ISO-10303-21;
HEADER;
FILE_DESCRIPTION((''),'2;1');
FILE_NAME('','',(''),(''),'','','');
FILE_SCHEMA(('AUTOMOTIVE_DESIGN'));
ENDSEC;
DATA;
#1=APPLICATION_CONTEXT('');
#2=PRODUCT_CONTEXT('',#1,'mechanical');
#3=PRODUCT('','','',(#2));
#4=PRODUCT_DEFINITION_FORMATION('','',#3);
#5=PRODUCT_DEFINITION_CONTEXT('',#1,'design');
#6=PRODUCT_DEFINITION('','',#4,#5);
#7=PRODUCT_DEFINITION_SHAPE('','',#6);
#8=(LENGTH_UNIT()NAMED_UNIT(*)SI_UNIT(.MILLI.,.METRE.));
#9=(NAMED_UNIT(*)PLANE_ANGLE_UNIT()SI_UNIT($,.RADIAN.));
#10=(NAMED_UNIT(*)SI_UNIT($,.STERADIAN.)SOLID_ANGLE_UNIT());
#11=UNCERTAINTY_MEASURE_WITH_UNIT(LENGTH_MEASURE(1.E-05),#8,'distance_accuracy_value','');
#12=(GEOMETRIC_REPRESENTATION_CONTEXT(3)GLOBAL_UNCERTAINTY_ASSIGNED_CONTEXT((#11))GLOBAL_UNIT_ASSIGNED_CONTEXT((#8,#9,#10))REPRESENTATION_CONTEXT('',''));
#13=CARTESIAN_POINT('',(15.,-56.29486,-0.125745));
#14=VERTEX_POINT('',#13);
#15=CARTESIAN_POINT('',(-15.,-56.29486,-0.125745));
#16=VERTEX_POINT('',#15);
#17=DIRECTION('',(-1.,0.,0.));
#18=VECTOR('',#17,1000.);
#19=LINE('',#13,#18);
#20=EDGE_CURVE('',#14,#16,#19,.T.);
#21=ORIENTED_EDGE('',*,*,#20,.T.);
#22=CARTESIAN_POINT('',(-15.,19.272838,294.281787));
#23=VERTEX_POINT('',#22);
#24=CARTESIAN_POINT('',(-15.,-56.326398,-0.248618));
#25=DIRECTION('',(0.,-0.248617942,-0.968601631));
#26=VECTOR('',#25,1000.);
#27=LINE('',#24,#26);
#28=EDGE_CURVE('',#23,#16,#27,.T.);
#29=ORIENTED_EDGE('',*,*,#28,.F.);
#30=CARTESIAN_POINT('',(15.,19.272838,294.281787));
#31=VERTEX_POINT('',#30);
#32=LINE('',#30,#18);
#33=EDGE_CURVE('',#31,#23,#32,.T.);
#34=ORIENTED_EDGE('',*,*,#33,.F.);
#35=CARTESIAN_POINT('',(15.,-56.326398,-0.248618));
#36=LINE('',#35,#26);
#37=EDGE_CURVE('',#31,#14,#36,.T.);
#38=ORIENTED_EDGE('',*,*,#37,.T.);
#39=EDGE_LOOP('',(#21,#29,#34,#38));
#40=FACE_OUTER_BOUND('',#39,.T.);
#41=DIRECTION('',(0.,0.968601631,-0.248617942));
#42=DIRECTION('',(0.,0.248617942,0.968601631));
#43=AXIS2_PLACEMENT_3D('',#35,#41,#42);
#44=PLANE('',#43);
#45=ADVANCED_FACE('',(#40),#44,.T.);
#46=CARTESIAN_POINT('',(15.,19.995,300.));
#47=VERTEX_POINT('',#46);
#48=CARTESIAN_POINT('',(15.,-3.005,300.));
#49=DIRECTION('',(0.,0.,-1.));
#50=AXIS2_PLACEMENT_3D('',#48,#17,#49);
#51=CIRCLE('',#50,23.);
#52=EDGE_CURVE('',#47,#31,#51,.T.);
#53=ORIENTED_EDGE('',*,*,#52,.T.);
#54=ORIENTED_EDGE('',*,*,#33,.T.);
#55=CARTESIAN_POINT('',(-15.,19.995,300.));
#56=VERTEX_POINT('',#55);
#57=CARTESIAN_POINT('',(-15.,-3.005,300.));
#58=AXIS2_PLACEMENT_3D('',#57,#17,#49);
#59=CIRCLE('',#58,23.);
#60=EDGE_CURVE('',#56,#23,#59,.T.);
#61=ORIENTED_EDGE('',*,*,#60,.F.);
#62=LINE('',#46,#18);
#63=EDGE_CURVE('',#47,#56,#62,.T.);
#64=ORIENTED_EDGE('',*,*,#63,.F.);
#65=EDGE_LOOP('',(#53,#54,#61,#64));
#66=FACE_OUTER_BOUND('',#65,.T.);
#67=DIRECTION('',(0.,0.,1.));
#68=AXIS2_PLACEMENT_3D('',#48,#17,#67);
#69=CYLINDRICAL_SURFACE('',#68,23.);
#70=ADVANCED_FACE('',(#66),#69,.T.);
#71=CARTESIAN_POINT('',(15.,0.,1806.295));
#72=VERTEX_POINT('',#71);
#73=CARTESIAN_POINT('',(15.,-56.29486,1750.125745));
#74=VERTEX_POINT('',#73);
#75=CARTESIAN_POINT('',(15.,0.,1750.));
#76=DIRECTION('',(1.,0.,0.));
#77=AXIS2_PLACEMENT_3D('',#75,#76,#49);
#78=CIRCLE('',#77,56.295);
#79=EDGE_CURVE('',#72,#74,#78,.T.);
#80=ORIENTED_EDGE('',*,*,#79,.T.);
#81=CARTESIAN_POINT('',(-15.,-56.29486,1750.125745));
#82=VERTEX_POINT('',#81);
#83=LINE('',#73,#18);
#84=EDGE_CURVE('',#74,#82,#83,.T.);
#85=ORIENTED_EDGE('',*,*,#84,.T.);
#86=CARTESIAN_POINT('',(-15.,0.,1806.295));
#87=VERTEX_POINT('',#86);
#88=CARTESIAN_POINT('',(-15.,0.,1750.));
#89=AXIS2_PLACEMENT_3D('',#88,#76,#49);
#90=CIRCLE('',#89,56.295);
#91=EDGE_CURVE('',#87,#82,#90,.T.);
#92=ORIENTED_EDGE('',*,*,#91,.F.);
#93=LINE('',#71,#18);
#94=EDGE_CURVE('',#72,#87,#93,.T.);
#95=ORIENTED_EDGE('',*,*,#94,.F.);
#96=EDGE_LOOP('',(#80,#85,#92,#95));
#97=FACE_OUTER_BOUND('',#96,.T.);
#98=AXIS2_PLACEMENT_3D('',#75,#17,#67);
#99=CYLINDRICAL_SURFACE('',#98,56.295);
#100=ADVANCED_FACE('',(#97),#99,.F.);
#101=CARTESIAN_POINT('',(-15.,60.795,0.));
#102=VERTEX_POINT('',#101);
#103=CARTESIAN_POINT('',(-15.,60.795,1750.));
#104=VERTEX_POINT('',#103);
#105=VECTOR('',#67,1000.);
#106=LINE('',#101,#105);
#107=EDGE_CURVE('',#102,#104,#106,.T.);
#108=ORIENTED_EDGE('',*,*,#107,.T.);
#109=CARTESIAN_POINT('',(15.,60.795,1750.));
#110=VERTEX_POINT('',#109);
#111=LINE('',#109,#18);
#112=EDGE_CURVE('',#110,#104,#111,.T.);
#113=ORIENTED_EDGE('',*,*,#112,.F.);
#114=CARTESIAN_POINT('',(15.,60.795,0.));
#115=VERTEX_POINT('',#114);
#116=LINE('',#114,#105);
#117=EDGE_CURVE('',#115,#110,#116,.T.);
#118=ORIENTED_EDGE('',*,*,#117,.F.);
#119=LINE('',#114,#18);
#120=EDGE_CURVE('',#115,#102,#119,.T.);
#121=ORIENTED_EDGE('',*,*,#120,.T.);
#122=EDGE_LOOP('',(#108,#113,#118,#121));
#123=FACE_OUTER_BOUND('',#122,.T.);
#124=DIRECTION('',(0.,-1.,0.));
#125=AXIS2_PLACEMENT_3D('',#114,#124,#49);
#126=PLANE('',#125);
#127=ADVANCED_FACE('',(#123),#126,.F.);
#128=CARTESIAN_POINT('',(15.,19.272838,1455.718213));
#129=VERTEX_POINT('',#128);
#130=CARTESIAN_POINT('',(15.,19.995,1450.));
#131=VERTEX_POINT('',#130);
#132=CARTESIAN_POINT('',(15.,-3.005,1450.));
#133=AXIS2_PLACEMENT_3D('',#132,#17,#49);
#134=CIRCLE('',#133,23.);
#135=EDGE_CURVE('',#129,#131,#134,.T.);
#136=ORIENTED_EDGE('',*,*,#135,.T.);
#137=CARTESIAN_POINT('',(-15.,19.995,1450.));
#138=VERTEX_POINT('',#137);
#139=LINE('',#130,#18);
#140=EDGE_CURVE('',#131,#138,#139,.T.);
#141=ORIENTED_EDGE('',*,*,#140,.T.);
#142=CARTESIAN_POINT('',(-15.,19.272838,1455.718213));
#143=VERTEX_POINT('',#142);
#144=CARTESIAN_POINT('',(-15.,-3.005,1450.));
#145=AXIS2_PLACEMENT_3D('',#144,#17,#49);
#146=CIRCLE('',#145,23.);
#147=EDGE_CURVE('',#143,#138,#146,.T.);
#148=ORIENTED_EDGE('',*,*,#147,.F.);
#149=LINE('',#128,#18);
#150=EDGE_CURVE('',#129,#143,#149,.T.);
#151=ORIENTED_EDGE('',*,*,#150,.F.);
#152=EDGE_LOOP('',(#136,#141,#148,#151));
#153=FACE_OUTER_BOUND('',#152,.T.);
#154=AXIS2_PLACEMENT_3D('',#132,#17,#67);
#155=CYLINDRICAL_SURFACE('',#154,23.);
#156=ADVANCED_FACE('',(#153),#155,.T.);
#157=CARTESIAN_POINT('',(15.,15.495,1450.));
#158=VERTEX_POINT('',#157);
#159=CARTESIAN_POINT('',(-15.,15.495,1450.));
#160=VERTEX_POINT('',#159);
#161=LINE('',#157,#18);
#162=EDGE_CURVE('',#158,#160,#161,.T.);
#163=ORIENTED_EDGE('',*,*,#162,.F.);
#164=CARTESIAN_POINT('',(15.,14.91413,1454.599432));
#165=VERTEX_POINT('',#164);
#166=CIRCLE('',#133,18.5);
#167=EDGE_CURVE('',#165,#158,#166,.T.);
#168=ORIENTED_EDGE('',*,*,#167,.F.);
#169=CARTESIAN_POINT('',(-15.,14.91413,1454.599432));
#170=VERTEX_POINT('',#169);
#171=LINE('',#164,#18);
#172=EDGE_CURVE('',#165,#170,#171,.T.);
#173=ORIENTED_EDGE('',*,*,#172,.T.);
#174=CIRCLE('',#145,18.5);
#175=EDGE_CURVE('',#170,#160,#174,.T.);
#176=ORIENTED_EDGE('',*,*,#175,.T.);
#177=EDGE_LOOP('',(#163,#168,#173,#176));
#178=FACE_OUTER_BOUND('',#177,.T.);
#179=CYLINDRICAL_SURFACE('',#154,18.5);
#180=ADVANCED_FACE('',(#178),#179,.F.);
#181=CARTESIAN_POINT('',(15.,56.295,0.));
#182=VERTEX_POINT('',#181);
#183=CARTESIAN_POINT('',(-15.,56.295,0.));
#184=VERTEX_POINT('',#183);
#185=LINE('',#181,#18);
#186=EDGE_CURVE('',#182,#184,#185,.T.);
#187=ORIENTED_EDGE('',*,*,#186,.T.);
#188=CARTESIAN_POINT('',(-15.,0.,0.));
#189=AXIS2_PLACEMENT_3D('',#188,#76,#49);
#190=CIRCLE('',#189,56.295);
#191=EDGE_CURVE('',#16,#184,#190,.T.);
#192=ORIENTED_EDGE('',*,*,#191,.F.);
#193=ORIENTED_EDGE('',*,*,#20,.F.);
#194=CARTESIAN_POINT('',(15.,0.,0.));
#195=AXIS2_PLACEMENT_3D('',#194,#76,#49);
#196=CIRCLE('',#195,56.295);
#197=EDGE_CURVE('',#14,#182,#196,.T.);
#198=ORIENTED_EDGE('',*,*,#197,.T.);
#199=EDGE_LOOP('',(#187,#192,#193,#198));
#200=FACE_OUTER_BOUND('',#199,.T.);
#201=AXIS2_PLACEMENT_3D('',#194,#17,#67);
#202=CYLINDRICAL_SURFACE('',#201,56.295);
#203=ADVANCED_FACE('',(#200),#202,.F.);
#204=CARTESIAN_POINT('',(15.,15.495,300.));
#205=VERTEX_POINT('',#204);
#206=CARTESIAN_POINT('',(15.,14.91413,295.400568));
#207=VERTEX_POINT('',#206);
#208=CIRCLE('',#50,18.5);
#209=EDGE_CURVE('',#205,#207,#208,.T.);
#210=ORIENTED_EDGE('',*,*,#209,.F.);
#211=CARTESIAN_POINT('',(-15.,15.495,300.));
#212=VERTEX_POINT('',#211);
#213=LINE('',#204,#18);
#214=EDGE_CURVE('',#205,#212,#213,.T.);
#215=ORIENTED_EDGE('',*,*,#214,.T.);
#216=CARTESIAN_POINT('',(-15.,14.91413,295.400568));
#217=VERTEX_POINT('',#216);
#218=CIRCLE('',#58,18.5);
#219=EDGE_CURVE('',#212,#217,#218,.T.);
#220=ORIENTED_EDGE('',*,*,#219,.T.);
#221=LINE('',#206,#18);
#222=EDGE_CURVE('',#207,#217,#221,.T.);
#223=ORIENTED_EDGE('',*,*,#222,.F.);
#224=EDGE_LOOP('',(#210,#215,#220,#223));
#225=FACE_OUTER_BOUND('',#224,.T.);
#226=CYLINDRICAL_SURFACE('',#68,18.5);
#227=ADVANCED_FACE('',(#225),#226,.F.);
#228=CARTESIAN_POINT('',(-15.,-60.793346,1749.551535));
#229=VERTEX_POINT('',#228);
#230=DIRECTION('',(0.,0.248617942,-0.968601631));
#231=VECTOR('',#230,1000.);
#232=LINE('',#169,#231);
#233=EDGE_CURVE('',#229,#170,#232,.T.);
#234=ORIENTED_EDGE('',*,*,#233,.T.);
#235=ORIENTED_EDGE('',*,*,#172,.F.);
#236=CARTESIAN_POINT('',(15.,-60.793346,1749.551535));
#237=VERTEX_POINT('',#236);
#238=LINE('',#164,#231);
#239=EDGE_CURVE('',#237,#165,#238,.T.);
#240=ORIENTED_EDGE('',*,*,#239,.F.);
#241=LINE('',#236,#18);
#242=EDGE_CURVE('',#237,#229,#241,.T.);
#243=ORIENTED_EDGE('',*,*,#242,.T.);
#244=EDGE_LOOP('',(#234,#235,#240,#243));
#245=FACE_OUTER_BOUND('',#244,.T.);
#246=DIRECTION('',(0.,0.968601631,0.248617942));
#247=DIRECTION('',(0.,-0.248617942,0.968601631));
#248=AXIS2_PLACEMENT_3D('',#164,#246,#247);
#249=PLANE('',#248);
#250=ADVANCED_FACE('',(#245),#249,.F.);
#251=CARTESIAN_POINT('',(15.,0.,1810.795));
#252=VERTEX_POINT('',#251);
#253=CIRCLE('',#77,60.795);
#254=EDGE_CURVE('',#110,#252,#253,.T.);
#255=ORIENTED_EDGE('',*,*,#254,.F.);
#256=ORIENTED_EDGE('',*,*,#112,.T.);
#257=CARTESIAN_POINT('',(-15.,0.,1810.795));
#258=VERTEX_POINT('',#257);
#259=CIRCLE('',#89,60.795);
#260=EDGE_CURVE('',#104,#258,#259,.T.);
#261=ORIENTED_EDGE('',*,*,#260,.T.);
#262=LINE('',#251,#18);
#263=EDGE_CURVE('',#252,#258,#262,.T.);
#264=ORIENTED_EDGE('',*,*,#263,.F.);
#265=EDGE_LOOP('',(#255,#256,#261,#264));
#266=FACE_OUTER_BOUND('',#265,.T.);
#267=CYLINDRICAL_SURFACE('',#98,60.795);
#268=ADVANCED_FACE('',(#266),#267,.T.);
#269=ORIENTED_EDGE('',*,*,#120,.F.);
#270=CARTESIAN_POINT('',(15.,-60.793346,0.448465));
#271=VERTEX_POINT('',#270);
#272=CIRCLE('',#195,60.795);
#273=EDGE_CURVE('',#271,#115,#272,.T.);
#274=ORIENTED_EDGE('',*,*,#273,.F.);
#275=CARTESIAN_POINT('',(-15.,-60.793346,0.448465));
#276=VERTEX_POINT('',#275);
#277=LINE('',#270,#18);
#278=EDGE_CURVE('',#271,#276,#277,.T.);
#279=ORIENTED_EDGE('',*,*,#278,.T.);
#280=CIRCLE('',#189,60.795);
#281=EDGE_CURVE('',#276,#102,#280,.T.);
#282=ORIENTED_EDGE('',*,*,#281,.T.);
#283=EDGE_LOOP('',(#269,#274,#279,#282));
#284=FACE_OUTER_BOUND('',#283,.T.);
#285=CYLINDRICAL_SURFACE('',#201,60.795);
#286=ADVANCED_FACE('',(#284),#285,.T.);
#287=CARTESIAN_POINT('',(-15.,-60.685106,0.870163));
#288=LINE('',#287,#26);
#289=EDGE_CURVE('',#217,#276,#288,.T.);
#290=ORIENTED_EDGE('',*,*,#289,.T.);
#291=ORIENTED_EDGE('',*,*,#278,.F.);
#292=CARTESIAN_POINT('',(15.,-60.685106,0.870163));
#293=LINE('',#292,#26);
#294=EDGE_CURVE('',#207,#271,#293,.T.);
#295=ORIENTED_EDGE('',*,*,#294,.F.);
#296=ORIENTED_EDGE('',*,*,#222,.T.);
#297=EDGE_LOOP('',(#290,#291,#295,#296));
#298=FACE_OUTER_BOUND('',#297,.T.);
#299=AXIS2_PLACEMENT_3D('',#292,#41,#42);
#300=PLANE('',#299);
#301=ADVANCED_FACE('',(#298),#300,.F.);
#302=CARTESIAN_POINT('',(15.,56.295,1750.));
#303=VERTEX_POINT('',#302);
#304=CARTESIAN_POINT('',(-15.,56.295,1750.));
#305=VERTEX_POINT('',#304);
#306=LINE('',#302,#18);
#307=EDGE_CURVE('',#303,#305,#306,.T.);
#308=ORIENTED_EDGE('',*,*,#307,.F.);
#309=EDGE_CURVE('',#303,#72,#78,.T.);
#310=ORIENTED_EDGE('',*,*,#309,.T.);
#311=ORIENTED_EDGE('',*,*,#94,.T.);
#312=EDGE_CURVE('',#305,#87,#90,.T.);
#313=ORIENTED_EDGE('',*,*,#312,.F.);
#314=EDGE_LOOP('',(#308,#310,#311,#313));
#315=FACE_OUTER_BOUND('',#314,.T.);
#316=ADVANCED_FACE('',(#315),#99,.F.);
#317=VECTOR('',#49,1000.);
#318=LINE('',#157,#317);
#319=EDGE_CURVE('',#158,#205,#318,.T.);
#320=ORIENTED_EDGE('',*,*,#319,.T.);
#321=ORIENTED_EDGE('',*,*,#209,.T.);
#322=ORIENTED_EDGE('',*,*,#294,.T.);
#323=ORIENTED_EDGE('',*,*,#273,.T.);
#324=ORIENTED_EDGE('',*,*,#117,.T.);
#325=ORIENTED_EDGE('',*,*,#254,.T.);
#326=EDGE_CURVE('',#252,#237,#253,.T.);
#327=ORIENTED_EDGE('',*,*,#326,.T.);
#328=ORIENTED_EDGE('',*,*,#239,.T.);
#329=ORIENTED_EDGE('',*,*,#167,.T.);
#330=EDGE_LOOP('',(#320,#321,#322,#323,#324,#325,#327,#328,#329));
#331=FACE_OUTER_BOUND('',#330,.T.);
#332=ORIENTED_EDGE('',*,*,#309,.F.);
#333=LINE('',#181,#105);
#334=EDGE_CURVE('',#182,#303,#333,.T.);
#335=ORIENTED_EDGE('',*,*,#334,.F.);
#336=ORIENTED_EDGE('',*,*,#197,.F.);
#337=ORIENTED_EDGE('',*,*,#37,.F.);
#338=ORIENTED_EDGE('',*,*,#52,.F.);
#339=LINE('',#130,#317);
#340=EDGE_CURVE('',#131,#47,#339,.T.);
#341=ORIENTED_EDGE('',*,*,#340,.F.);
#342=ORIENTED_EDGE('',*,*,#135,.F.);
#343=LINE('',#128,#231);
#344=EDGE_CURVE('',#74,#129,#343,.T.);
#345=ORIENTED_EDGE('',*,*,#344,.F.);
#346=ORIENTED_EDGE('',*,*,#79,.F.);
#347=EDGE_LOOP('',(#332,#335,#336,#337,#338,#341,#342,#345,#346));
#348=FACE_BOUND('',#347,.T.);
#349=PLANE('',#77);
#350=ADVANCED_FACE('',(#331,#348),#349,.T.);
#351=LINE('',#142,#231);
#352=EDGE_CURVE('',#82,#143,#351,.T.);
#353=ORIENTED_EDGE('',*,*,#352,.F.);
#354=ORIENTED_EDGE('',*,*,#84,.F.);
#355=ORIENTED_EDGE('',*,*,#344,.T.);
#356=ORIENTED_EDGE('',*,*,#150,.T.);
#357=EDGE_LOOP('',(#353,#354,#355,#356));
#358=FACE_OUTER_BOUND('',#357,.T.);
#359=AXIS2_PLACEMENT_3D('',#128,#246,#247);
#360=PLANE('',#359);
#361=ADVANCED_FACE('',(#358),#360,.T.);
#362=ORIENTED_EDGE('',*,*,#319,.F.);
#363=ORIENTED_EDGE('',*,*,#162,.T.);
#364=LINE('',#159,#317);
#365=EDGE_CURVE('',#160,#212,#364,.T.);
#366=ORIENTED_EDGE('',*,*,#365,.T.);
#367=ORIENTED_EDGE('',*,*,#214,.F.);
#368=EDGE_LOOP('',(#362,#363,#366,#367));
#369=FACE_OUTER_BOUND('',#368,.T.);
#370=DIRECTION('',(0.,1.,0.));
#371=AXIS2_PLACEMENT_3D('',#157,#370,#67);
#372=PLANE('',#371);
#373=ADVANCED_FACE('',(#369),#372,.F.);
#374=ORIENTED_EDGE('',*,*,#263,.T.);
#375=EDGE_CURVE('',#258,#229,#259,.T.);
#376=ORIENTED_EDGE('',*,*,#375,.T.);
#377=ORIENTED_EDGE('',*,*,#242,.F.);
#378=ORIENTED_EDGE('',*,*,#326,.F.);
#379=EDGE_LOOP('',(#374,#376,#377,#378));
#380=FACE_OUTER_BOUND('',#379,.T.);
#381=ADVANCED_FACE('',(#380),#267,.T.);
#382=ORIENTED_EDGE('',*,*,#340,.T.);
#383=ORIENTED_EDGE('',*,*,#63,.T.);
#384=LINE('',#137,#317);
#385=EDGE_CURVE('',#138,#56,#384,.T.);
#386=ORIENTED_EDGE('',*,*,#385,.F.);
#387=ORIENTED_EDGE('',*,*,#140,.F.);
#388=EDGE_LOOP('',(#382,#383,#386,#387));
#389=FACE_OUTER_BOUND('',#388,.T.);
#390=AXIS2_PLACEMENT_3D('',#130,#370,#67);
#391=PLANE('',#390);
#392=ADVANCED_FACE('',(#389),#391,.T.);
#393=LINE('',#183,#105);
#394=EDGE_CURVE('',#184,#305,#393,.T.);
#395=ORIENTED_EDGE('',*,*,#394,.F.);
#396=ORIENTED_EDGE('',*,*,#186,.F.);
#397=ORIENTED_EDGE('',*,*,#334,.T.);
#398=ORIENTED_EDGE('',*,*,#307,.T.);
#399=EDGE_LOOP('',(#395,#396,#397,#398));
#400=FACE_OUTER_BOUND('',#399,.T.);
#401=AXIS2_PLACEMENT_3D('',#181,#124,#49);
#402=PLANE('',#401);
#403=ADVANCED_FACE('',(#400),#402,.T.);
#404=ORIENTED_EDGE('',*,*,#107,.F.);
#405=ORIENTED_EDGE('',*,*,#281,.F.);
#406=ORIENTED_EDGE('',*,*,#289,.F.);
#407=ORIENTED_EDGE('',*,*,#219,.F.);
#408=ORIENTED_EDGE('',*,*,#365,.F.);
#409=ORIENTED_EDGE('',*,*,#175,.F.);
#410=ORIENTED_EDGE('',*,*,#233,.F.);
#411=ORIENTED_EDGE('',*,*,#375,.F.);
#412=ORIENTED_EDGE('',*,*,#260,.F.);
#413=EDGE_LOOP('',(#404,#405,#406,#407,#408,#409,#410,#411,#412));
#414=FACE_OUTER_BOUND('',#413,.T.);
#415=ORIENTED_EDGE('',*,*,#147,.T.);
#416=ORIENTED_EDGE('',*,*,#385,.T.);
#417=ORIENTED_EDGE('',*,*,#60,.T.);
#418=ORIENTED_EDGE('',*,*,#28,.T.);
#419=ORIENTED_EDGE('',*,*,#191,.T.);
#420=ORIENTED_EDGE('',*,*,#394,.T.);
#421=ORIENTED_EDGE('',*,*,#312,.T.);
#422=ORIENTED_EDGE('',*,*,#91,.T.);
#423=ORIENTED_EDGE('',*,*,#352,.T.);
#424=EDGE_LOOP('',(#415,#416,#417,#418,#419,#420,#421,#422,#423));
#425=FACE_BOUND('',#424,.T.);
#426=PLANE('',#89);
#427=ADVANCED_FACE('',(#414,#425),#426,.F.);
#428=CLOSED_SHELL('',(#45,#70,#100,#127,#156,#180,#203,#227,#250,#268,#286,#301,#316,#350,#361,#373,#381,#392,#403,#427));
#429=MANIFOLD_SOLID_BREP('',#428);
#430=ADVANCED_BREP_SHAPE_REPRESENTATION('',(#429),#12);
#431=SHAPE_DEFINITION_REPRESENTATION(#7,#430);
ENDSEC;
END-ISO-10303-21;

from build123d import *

# Parameters (mm, degrees)
EXTRUDE_1_DEPTH = 15


with BuildPart() as part:
    # 草图2 → 拉伸-薄壁1 (new, symmetric)
    with BuildSketch(Plane(origin=(0, 0, 0), x_dir=(0, 0, -1), z_dir=(1, 0, 0))):
        with BuildLine():
            Line((-295.400568077, 14.914130168), (-0.448465098, -60.793345886))
            ThreePointArc((-0.448465098, -60.793345886), (60.79458647, -0.224234074), (0, 60.795))
            Line((0, 60.795), (-1750, 60.795))
            ThreePointArc((-1750, 60.795), (-1810.79458647, -0.224234074), (-1749.551534902, -60.793345886))
            Line((-1749.551534902, -60.793345886), (-1454.599431923, 14.914130168))
            ThreePointArc((-1454.599431923, 14.914130168), (-1452.317983163, 15.349208075), (-1450, 15.495))
            Line((-1450, 15.495), (-300, 15.495))
            ThreePointArc((-300, 15.495), (-297.682016837, 15.349208075), (-295.400568077, 14.914130168))
        make_face()
        with BuildLine():
            Line((-294.281787339, 19.272837507), (0.125744515, -56.294859564))
            ThreePointArc((0.125744515, -56.294859564), (56.294964891, 0.062872297), (0, 56.295))
            Line((0, 56.295), (-1750, 56.295))
            ThreePointArc((-1750, 56.295), (-1806.294964891, 0.062872297), (-1750.125744515, -56.294859564))
            Line((-1750.125744515, -56.294859564), (-1455.718212661, 19.272837507))
            ThreePointArc((-1455.718212661, 19.272837507), (-1452.881816905, 19.813745174), (-1450, 19.995))
            Line((-1450, 19.995), (-300, 19.995))
            ThreePointArc((-300, 19.995), (-297.118183095, 19.813745174), (-294.281787339, 19.272837507))
        make_face(mode=Mode.SUBTRACT)
    extrude(amount=EXTRUDE_1_DEPTH, both=True)


solid = part.part
